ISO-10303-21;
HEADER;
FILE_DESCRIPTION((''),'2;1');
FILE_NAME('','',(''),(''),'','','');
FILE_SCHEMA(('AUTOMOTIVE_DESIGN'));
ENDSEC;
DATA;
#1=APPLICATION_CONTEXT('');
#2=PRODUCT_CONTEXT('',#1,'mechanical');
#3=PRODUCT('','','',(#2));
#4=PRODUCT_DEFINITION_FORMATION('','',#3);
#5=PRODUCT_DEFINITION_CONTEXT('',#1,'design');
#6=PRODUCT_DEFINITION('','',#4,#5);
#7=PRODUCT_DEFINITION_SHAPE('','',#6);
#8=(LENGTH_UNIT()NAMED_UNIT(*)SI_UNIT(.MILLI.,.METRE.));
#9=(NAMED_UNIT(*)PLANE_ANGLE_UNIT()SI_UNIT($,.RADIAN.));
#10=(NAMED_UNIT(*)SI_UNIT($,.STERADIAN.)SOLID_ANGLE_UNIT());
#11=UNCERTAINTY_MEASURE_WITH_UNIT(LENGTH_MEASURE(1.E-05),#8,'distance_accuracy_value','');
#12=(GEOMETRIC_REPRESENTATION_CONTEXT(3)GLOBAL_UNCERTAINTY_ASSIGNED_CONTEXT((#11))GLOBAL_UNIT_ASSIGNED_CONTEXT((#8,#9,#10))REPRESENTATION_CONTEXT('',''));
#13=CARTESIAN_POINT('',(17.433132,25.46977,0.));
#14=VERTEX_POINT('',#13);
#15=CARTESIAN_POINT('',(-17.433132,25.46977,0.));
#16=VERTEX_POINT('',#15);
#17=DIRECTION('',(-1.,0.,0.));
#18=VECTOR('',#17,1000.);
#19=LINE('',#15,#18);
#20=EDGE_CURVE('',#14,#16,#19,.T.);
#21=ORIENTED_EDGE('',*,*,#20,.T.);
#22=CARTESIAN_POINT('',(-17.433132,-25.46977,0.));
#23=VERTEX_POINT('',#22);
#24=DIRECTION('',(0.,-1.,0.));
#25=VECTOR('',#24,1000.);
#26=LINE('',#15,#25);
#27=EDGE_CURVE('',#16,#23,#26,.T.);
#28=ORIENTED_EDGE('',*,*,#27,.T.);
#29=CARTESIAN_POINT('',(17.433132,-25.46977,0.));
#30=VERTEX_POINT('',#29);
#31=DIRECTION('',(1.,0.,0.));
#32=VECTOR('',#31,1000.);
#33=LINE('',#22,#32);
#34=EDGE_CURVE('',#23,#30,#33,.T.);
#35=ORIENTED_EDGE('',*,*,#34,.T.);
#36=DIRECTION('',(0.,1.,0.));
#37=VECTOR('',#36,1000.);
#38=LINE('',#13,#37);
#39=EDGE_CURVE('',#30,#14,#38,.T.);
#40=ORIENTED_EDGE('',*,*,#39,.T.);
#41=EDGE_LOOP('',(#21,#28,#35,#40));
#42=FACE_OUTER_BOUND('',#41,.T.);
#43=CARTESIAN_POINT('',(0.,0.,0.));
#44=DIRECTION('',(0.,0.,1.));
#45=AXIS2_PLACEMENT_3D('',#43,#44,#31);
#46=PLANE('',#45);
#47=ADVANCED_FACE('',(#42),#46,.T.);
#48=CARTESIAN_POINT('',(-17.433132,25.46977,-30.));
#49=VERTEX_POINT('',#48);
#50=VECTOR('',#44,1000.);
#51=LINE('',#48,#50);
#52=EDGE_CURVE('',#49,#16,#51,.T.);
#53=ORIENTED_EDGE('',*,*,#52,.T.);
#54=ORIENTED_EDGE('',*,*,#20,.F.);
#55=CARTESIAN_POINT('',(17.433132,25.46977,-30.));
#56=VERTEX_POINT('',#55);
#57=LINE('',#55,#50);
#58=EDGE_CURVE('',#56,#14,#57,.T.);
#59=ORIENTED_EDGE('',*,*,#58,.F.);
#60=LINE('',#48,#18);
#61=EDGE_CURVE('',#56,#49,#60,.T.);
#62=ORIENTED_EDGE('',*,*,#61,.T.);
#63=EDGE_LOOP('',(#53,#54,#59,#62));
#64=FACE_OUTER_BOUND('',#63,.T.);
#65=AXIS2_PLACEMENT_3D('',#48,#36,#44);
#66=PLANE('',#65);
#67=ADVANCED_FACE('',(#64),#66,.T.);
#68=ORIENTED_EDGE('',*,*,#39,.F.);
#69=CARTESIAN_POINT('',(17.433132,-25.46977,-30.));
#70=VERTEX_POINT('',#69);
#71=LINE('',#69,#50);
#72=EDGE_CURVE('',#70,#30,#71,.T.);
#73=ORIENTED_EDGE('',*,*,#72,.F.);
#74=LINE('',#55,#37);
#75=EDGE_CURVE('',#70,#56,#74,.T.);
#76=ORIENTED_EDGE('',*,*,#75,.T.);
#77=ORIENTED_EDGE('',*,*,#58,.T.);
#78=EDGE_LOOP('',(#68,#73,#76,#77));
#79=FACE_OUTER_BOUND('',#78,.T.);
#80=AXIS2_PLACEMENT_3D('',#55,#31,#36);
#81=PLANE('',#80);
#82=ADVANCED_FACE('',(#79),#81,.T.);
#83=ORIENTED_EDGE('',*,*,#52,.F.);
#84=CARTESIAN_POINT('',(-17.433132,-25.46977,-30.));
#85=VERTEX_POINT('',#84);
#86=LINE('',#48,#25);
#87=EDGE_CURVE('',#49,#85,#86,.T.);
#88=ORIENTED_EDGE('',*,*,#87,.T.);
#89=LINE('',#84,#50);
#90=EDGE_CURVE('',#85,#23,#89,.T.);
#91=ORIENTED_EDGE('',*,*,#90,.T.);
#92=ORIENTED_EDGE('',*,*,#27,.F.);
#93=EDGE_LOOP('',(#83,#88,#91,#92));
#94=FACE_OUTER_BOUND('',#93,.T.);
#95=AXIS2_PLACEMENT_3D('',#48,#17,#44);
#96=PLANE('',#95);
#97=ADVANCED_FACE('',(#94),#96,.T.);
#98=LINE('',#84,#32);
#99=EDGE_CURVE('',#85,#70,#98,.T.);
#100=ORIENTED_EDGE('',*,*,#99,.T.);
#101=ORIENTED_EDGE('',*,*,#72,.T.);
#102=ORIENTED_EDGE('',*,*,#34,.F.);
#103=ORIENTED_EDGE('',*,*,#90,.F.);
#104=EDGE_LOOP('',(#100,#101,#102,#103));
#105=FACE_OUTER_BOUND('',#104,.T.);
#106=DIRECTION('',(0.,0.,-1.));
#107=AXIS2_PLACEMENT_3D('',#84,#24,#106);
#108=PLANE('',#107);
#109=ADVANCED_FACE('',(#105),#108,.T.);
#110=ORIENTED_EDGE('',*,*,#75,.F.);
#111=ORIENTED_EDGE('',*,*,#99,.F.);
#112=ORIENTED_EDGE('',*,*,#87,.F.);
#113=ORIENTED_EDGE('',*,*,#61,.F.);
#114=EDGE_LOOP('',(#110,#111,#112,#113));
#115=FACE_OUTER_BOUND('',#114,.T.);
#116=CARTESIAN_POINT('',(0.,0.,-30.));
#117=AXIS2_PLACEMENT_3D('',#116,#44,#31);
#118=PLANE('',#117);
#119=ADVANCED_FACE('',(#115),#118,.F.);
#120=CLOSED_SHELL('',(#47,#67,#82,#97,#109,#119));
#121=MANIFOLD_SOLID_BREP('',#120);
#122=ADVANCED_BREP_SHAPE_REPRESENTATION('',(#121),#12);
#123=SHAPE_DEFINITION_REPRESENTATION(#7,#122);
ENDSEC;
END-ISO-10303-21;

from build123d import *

# Parameters (mm, degrees)
SKETCH1_W           = 34.866263656
SKETCH1_H           = 50.939540762
BOSS_EXTRUDE1_DEPTH = 30


with BuildPart() as part:
    # Sketch1 → Boss-Extrude1 (new body)
    with BuildSketch(Plane.XY):
        Rectangle(SKETCH1_W, SKETCH1_H)
    extrude(amount=-BOSS_EXTRUDE1_DEPTH)


solid = part.part
